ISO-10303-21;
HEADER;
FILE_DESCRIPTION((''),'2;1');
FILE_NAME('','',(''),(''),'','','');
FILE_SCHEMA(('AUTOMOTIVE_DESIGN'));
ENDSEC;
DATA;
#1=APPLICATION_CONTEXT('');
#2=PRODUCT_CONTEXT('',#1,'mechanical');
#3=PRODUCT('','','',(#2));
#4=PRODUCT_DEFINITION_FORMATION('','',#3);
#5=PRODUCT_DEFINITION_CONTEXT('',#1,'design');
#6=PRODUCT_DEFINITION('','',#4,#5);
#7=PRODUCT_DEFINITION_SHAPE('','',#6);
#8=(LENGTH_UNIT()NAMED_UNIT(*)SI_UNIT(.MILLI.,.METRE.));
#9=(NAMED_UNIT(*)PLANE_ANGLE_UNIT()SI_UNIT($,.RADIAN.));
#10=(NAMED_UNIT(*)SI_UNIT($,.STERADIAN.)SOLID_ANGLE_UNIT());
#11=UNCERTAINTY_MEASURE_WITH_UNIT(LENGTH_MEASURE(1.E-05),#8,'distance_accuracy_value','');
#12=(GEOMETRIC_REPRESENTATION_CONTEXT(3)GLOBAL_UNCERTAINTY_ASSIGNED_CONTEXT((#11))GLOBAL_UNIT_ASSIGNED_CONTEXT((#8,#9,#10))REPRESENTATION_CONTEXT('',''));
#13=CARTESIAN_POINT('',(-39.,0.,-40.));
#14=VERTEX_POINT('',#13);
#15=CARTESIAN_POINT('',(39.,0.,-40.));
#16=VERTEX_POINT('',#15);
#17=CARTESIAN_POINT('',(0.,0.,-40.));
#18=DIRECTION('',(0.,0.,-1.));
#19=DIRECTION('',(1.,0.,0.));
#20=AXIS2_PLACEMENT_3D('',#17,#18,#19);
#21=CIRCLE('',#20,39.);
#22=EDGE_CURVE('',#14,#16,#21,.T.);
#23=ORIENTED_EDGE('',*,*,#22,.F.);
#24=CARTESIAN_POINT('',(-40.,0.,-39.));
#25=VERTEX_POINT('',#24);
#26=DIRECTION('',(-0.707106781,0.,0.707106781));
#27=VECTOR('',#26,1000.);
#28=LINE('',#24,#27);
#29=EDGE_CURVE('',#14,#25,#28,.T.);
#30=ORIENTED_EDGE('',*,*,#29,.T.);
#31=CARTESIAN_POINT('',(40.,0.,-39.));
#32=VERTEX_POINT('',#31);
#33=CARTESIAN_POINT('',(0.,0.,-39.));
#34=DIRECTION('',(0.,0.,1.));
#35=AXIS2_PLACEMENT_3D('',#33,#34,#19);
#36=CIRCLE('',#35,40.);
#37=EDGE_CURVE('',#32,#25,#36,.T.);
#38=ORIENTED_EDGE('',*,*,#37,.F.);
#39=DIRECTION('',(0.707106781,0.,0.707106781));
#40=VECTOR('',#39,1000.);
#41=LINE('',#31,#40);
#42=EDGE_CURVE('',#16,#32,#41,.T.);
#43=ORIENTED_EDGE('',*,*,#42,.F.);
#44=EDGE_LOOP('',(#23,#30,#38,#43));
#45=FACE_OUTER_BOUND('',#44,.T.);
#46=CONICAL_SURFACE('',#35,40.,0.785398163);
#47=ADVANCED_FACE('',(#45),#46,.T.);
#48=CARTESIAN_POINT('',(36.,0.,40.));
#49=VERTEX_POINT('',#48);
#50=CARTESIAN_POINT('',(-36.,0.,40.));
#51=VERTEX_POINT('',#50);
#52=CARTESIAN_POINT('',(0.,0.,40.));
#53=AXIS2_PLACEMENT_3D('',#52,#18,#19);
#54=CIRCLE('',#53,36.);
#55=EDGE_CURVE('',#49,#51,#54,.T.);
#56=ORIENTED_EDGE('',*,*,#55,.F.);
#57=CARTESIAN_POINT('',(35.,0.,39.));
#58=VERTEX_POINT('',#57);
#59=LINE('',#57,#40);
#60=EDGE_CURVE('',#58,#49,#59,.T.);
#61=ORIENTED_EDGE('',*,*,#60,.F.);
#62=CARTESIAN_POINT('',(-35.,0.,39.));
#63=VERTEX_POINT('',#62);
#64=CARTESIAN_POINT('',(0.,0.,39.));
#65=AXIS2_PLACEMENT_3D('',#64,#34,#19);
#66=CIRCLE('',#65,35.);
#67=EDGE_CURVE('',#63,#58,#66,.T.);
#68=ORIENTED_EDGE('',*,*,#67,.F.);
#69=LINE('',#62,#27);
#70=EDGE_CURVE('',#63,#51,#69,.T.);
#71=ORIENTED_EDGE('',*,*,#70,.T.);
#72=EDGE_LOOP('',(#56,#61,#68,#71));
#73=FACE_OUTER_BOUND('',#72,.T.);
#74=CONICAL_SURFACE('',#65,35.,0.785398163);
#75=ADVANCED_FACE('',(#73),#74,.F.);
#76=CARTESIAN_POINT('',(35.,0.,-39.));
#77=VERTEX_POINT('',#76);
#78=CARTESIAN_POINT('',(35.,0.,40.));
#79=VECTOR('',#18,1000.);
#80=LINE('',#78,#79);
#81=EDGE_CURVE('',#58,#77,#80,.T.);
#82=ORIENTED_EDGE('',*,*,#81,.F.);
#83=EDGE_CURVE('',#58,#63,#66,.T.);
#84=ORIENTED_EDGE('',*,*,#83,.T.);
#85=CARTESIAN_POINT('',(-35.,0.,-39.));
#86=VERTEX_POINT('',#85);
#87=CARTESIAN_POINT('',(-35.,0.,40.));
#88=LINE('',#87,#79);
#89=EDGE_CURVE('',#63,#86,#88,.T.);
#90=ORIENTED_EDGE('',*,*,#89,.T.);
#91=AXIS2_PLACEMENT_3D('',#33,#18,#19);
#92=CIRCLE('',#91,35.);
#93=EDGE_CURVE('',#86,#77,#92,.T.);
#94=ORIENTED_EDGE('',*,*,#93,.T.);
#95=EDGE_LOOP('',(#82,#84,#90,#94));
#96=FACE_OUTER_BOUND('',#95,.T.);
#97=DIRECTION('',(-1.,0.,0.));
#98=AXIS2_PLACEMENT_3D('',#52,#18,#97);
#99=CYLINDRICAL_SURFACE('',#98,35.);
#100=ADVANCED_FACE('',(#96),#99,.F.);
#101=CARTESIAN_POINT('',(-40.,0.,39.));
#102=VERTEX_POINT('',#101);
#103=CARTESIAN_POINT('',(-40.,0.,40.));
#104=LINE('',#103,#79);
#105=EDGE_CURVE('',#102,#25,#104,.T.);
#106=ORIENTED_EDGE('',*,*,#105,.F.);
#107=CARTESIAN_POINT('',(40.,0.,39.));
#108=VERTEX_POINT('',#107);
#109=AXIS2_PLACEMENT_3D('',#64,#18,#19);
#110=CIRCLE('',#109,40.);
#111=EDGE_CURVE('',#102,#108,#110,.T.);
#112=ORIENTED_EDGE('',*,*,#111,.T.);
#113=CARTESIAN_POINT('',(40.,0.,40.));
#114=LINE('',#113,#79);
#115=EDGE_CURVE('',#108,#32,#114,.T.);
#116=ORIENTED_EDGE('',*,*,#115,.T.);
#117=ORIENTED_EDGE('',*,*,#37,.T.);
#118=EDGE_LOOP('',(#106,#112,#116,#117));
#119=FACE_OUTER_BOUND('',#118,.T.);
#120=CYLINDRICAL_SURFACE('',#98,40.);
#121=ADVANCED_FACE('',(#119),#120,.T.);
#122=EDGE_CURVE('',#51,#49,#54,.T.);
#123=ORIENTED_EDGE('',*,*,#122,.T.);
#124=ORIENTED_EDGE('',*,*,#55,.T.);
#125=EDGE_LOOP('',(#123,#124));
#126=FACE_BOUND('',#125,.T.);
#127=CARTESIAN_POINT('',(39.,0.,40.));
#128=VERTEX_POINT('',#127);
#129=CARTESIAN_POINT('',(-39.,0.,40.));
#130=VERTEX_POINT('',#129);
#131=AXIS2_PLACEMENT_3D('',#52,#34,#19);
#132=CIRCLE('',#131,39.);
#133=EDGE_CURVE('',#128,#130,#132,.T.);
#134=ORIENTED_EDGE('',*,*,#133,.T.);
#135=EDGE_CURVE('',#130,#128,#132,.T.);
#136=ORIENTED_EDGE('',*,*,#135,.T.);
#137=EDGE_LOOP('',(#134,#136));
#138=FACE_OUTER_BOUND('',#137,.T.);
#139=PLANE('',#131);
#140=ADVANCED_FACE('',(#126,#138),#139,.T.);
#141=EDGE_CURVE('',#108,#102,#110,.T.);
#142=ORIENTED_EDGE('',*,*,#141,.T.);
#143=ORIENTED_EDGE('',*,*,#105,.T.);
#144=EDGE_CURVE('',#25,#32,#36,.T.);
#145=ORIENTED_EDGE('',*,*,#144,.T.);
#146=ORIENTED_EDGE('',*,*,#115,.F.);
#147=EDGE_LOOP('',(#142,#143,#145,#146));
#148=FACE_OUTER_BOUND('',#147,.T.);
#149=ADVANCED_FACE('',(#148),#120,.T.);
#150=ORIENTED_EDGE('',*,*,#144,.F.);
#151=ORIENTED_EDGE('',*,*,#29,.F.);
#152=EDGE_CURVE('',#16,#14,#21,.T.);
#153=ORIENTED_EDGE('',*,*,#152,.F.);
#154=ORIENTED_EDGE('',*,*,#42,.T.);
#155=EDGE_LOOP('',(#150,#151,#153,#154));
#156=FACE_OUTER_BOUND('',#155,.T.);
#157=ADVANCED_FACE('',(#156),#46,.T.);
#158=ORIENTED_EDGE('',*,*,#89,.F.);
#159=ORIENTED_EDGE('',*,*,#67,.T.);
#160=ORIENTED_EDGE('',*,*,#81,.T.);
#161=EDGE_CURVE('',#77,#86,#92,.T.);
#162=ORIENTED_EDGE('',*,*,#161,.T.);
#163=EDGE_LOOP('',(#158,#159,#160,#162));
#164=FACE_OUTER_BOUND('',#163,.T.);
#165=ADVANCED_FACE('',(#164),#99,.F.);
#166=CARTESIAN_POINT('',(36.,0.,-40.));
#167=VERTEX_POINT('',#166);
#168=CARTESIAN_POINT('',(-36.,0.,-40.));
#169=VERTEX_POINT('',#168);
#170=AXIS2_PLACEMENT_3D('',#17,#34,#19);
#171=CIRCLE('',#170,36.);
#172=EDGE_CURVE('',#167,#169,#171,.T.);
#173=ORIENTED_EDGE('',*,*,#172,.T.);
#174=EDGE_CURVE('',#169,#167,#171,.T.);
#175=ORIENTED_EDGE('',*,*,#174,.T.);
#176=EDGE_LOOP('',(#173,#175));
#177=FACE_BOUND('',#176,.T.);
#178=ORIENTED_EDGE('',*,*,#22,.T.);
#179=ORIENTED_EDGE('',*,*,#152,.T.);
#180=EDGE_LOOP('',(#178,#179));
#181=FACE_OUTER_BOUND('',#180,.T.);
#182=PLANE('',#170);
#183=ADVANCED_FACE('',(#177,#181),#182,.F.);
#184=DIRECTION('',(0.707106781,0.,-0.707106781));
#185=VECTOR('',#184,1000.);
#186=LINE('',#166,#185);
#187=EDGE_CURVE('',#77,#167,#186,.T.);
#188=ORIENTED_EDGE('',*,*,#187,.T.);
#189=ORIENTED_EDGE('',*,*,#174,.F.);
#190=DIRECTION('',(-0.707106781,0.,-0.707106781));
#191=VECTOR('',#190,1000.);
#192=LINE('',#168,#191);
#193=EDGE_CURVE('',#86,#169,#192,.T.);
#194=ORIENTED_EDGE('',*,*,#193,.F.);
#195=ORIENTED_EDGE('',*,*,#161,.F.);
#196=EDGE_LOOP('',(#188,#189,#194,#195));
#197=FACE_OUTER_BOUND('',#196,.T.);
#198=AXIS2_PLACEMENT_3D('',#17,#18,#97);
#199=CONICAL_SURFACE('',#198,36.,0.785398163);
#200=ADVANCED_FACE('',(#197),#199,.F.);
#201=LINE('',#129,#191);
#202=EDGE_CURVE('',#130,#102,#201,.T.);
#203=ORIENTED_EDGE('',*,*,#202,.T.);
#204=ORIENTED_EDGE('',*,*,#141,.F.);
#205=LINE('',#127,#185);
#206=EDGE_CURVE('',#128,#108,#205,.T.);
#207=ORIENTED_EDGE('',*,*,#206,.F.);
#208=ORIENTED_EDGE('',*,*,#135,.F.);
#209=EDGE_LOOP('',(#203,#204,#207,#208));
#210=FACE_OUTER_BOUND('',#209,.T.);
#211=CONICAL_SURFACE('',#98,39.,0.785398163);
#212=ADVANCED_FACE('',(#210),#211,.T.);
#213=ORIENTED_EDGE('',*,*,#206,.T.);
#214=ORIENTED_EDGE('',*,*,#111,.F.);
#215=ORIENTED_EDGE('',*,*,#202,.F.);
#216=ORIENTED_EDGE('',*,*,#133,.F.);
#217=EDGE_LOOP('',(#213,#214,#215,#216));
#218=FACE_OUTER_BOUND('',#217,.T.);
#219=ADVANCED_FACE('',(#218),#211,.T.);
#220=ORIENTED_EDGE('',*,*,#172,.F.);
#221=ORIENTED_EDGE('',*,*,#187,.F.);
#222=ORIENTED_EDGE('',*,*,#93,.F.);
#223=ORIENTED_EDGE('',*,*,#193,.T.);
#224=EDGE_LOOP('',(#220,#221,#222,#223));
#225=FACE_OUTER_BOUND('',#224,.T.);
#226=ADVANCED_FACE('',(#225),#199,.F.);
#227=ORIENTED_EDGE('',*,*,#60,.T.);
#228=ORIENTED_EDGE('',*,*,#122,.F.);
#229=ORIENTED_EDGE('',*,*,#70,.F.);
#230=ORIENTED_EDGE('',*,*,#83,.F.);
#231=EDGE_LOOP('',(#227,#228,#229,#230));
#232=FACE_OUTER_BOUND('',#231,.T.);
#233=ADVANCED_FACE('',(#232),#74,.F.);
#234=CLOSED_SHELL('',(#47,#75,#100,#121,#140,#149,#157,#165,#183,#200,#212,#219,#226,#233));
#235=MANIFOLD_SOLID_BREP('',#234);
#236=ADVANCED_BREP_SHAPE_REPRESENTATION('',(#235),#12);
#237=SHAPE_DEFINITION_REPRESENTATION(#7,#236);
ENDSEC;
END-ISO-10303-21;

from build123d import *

# Parameters (mm, degrees)
SKETCH1_R           = 40
SKETCH1_R_2         = 35
BOSS_EXTRUDE1_DEPTH = 40
CHAMFER1_SIZE       = 1


with BuildPart() as part:
    # Sketch1 → Boss-Extrude1 (new, symmetric)
    with BuildSketch(Plane.XY):
        Circle(SKETCH1_R)
        Circle(SKETCH1_R_2, mode=Mode.SUBTRACT)
    extrude(amount=BOSS_EXTRUDE1_DEPTH, both=True)

    # Chamfer1
    chamfer1_edges = [part.edges().sort_by_distance(p)[0] for p in [
        (-40, 0, -40),
        (-40, 0, 40),
        (-35, 0, -40),
        (-35, 0, 40),
    ]]
    chamfer(chamfer1_edges, length=CHAMFER1_SIZE)


solid = part.part
